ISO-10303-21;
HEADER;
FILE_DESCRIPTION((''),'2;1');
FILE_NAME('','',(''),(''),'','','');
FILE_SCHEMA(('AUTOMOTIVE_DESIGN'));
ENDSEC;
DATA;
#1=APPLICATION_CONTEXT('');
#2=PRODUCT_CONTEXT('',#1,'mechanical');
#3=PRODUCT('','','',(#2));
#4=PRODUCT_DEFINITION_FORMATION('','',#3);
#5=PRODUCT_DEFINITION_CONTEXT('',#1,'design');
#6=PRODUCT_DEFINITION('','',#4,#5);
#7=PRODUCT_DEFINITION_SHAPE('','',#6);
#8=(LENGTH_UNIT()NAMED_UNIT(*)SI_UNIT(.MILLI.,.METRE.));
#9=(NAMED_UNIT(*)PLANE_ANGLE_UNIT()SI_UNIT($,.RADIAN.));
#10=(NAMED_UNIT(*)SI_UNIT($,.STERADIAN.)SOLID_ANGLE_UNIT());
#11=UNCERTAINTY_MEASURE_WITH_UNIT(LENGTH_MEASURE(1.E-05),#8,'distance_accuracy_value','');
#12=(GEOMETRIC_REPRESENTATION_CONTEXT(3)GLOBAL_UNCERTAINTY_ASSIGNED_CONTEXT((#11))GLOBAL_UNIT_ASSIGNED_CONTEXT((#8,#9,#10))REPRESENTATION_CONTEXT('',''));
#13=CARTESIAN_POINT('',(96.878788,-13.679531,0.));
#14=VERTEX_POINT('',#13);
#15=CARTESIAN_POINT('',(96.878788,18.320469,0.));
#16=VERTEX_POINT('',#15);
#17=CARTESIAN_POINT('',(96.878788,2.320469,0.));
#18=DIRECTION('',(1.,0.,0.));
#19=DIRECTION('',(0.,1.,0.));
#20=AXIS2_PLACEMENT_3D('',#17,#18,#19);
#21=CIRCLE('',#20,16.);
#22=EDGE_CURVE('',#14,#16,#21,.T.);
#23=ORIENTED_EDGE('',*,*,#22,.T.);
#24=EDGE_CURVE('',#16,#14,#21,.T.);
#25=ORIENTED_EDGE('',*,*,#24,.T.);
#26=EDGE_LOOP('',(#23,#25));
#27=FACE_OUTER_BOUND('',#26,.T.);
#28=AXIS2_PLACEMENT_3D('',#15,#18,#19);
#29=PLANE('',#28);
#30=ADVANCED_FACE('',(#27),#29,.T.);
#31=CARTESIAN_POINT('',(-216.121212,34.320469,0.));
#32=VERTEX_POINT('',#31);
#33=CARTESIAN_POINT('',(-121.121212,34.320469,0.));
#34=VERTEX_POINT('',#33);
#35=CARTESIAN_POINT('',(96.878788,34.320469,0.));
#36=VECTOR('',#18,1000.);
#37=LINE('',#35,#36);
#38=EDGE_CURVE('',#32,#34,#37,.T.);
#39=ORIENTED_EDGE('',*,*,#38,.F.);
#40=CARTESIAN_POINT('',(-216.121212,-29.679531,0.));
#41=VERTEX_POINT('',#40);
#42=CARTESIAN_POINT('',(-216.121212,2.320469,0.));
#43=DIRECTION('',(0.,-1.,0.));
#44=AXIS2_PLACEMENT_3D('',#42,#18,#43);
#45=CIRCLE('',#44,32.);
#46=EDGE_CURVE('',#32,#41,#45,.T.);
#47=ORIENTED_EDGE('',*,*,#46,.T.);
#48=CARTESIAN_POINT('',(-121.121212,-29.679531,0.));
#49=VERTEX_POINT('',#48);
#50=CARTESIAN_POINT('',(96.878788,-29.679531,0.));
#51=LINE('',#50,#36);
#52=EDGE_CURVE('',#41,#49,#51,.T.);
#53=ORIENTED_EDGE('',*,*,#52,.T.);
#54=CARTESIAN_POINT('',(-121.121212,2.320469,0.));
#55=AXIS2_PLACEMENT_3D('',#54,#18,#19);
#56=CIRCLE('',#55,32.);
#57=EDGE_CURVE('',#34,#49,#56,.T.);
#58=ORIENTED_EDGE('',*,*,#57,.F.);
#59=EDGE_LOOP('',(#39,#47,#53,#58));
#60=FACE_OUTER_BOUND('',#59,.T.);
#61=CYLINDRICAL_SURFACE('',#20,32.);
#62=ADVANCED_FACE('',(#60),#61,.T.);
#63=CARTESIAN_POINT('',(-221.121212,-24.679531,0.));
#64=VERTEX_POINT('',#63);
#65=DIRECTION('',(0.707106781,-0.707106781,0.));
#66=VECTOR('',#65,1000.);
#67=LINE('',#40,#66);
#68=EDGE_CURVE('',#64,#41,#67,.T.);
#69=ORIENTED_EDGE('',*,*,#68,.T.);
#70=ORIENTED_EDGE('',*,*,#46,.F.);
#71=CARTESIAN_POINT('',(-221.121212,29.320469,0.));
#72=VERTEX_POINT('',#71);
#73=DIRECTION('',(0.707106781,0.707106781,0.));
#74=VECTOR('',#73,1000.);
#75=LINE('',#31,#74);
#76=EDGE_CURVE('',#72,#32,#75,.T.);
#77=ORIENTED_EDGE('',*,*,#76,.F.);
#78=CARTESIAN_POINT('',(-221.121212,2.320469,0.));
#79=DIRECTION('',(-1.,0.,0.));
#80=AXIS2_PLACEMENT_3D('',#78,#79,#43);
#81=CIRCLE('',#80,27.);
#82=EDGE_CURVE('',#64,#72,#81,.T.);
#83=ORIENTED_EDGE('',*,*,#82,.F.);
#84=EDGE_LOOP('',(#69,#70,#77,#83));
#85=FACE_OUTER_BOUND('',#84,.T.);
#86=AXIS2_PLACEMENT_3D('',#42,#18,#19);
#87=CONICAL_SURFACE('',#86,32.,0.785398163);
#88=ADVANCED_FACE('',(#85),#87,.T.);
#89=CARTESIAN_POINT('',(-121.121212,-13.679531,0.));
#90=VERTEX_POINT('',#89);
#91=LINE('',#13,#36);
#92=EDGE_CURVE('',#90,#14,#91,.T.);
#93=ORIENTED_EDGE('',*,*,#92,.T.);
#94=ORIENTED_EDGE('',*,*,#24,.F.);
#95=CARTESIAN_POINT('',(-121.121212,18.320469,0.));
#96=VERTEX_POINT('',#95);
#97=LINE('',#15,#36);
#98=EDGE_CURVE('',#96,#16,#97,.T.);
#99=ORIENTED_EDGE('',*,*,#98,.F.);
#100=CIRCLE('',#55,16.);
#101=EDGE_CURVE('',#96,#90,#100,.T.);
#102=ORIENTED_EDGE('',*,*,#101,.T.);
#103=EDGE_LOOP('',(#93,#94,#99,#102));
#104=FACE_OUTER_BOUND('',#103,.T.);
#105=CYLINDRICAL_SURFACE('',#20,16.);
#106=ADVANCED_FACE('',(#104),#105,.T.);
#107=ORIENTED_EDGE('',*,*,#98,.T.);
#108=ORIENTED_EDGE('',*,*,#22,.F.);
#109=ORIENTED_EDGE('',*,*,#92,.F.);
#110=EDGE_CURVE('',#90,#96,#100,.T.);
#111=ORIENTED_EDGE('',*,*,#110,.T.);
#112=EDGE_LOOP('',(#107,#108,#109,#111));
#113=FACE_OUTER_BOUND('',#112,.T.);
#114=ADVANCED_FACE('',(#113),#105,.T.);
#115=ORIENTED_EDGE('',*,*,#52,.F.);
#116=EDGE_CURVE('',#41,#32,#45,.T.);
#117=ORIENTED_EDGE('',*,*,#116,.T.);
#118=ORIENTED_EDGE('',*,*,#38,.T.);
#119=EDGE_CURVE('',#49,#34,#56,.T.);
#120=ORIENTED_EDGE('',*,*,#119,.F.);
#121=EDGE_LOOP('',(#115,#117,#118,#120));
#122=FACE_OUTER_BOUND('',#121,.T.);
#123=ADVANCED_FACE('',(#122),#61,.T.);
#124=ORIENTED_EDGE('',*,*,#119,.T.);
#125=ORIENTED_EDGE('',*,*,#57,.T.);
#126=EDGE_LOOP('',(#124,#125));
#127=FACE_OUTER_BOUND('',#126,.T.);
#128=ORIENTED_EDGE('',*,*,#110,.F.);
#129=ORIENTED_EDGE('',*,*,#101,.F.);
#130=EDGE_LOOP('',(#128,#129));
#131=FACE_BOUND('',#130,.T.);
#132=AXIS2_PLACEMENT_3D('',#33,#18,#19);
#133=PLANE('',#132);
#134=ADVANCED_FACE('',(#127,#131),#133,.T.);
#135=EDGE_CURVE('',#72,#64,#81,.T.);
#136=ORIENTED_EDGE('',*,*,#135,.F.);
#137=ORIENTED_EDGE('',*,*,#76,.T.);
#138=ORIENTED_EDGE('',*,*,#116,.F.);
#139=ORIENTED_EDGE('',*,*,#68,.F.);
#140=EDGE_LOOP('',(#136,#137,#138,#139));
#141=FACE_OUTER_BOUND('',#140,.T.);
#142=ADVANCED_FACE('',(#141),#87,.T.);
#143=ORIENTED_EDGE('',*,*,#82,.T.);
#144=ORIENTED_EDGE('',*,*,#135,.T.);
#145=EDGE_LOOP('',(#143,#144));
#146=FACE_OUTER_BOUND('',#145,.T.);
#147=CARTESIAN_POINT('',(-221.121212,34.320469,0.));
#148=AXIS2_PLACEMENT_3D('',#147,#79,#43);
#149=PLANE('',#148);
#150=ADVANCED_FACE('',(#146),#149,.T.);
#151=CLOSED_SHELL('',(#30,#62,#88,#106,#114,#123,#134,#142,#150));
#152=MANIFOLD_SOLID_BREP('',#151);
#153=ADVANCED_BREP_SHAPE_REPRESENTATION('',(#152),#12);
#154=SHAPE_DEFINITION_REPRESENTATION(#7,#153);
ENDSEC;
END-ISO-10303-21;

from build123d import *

# Parameters (mm, degrees)
END_CHAMFER_5X45_SIZE = 5


with BuildPart() as part:
    # Shaft Profile → Shaft Body Revolve (revolve)
    with BuildSketch(Plane.XY):
        Polygon((96.878787879, 2.320468839), (-221.121212121, 2.320468839), (-221.121212121, 34.320468839), (-121.121212121, 34.320468839), (-121.121212121, 18.320468839), (96.878787879, 18.320468839), align=None)
    revolve(axis=Axis((96.878787879, 2.320468839, 0), (-1, 0, 0)))

    # End Chamfer 5x45°
    end_chamfer_5x45_edges = [part.edges().sort_by_distance(p)[0] for p in [
        (-221.121212121, -29.679531161, 0),
    ]]
    chamfer(end_chamfer_5x45_edges, length=END_CHAMFER_5X45_SIZE)


solid = part.part
